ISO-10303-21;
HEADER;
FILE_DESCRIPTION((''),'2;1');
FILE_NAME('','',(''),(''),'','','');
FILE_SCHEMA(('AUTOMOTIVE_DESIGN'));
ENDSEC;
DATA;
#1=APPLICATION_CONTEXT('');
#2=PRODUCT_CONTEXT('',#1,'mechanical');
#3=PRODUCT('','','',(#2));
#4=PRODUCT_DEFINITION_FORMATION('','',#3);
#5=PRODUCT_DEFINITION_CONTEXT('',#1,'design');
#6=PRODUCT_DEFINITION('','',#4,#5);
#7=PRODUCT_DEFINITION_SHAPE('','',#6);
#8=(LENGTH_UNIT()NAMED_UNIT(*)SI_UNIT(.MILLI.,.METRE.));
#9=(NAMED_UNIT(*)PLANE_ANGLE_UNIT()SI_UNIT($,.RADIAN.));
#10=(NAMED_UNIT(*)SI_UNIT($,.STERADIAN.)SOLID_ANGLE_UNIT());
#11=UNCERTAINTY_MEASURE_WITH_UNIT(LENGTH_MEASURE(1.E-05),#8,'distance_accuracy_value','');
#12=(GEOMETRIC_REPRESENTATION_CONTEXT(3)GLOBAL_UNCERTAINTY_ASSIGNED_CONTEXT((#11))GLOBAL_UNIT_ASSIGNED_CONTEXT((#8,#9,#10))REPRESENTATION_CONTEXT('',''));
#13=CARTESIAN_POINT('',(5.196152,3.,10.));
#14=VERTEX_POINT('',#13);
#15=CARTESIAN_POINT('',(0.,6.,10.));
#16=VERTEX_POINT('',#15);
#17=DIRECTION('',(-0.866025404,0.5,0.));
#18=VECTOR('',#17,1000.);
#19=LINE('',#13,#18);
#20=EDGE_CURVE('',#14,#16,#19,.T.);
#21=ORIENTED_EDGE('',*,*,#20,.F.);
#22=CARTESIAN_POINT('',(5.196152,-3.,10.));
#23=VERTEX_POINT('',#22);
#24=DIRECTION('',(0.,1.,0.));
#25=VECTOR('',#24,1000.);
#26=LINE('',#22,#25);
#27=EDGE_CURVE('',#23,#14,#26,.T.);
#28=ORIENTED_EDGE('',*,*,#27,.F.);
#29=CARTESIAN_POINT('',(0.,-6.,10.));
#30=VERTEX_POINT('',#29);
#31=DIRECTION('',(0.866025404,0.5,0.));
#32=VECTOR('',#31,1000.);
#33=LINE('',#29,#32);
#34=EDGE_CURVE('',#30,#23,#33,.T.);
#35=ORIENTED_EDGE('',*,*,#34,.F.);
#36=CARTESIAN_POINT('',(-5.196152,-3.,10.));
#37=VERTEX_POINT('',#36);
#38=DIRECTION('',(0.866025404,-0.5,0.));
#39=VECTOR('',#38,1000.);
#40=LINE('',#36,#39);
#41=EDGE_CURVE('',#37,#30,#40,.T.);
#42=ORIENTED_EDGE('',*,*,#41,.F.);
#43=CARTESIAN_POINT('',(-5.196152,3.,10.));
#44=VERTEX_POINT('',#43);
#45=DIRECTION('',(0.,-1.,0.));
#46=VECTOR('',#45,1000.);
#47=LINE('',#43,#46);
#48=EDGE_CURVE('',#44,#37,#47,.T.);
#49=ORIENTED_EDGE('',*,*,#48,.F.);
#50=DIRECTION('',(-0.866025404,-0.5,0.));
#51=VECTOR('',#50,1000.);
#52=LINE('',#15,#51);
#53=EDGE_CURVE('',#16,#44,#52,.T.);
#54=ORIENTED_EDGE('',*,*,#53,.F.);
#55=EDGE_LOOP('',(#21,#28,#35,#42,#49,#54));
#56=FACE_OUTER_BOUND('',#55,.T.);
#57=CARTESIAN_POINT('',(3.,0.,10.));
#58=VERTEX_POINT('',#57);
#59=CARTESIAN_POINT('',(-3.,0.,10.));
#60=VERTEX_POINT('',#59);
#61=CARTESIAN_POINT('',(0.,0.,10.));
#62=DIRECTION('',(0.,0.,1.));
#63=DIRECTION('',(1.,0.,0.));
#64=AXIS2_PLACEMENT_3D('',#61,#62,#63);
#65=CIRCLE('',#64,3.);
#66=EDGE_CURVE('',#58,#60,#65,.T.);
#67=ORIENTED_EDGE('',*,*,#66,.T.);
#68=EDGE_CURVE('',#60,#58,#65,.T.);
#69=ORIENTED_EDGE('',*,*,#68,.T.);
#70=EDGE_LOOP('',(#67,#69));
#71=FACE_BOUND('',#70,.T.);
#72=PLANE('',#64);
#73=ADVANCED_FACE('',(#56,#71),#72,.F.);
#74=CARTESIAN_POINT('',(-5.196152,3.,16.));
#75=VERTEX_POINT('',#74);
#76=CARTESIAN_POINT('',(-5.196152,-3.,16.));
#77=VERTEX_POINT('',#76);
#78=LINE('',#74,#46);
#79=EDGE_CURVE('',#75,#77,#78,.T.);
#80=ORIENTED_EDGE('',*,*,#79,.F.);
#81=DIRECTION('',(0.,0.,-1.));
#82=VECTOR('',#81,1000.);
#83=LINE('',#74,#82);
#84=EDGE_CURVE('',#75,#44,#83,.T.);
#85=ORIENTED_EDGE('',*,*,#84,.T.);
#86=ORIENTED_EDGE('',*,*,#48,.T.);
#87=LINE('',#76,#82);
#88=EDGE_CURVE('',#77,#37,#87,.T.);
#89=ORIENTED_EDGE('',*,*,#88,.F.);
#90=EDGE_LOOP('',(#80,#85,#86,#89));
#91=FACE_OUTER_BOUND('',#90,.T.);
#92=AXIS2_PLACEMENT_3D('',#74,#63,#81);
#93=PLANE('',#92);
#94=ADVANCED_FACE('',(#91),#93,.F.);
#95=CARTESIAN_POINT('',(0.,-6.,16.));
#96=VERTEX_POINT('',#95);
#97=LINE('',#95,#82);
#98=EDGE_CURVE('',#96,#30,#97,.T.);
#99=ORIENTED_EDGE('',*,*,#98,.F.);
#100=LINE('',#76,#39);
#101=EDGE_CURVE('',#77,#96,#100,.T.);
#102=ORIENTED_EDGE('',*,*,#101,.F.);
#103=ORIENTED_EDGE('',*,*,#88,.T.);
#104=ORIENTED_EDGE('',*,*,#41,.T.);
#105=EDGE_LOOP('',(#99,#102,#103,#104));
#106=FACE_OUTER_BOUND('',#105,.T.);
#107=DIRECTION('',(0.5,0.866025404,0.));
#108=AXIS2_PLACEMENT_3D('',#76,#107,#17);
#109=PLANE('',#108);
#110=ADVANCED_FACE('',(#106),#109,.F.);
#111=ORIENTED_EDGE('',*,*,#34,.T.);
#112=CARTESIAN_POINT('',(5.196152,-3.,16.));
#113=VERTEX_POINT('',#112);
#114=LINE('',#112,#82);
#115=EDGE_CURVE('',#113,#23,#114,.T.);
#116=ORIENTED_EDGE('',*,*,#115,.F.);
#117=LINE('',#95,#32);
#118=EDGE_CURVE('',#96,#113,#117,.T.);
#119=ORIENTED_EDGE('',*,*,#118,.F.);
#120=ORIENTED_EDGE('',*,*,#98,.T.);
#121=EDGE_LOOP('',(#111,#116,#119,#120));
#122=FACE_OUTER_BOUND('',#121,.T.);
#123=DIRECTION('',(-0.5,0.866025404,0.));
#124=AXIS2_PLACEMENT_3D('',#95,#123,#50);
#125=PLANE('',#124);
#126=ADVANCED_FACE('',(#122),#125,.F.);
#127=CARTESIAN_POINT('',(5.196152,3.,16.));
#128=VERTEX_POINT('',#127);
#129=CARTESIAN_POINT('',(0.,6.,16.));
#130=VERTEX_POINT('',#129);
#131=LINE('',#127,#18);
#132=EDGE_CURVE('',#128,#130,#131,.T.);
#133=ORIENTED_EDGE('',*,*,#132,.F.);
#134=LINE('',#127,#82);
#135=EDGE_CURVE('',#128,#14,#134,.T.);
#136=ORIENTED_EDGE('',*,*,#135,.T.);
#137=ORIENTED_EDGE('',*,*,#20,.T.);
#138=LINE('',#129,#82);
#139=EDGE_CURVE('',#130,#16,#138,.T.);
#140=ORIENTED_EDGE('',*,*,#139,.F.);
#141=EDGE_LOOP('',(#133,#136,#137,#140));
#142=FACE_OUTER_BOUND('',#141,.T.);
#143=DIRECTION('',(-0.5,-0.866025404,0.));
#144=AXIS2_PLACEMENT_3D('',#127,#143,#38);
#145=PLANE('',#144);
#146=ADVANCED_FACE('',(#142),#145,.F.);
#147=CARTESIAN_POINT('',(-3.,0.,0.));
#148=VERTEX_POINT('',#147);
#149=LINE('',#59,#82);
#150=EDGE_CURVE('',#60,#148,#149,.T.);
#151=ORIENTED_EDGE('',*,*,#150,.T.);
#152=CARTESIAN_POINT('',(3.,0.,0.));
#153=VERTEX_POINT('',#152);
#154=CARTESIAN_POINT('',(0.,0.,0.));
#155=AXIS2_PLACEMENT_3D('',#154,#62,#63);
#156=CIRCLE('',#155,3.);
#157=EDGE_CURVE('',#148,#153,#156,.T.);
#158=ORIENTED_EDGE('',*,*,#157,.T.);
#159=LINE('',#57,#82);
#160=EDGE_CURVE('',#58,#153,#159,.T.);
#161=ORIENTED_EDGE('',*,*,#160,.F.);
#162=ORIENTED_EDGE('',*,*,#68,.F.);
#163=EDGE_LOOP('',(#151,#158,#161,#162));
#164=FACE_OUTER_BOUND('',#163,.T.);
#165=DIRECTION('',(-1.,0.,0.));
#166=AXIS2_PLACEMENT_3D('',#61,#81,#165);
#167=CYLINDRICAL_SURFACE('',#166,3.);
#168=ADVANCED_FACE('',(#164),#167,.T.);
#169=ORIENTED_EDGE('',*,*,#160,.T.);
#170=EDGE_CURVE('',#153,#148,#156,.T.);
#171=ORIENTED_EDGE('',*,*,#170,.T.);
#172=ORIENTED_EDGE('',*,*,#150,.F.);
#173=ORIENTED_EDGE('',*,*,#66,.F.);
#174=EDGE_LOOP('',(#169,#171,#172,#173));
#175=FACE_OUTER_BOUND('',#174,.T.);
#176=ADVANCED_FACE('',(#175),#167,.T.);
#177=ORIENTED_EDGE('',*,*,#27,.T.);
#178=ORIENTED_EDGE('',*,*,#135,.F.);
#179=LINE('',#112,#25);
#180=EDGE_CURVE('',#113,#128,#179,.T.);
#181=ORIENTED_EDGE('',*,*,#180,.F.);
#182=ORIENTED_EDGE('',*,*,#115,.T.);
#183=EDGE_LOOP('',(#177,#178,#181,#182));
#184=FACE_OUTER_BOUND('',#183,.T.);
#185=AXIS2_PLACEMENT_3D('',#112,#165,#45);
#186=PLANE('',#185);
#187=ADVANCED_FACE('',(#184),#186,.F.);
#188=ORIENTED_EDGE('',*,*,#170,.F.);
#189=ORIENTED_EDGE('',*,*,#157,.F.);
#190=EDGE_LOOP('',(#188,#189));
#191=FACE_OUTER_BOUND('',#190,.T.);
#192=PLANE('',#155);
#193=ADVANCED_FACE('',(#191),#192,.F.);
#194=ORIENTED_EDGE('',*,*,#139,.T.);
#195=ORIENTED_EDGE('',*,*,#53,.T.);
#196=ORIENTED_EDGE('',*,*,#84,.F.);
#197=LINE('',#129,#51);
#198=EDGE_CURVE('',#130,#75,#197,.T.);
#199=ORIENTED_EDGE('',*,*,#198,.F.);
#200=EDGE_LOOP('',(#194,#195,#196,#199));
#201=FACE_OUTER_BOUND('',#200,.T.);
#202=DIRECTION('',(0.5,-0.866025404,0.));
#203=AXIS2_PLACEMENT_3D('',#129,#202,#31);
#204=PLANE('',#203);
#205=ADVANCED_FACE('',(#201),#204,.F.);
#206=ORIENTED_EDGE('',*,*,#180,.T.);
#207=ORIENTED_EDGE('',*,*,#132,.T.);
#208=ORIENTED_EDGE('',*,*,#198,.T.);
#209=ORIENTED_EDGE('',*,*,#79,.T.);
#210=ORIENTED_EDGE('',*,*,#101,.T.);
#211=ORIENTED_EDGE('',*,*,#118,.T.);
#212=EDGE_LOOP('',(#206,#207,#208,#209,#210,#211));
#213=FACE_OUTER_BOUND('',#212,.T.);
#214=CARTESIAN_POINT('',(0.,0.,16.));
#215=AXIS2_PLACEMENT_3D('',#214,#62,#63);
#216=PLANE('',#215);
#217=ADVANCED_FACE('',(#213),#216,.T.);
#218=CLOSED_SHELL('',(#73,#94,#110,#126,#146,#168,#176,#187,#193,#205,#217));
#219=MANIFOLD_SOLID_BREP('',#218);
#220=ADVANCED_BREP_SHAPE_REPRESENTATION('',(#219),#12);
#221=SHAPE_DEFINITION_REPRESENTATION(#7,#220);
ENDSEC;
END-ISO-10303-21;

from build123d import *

# Parameters (mm, degrees)
SKETCH1_R           = 3
BOSS_EXTRUDE1_DEPTH = 10
BOSS_EXTRUDE2_DEPTH = 6


with BuildPart() as part:
    # Sketch1 → Boss-Extrude1 (new body)
    with BuildSketch(Plane.XY):
        Circle(SKETCH1_R)
    extrude(amount=BOSS_EXTRUDE1_DEPTH)

    # Sketch2 → Boss-Extrude2 (add)
    with BuildSketch(Plane.XY.offset(10)):
        Polygon((-5.196152423, -3), (0, -6), (5.196152423, -3), (5.196152423, 3), (0, 6), (-5.196152423, 3), align=None)
    extrude(amount=BOSS_EXTRUDE2_DEPTH)


solid = part.part
